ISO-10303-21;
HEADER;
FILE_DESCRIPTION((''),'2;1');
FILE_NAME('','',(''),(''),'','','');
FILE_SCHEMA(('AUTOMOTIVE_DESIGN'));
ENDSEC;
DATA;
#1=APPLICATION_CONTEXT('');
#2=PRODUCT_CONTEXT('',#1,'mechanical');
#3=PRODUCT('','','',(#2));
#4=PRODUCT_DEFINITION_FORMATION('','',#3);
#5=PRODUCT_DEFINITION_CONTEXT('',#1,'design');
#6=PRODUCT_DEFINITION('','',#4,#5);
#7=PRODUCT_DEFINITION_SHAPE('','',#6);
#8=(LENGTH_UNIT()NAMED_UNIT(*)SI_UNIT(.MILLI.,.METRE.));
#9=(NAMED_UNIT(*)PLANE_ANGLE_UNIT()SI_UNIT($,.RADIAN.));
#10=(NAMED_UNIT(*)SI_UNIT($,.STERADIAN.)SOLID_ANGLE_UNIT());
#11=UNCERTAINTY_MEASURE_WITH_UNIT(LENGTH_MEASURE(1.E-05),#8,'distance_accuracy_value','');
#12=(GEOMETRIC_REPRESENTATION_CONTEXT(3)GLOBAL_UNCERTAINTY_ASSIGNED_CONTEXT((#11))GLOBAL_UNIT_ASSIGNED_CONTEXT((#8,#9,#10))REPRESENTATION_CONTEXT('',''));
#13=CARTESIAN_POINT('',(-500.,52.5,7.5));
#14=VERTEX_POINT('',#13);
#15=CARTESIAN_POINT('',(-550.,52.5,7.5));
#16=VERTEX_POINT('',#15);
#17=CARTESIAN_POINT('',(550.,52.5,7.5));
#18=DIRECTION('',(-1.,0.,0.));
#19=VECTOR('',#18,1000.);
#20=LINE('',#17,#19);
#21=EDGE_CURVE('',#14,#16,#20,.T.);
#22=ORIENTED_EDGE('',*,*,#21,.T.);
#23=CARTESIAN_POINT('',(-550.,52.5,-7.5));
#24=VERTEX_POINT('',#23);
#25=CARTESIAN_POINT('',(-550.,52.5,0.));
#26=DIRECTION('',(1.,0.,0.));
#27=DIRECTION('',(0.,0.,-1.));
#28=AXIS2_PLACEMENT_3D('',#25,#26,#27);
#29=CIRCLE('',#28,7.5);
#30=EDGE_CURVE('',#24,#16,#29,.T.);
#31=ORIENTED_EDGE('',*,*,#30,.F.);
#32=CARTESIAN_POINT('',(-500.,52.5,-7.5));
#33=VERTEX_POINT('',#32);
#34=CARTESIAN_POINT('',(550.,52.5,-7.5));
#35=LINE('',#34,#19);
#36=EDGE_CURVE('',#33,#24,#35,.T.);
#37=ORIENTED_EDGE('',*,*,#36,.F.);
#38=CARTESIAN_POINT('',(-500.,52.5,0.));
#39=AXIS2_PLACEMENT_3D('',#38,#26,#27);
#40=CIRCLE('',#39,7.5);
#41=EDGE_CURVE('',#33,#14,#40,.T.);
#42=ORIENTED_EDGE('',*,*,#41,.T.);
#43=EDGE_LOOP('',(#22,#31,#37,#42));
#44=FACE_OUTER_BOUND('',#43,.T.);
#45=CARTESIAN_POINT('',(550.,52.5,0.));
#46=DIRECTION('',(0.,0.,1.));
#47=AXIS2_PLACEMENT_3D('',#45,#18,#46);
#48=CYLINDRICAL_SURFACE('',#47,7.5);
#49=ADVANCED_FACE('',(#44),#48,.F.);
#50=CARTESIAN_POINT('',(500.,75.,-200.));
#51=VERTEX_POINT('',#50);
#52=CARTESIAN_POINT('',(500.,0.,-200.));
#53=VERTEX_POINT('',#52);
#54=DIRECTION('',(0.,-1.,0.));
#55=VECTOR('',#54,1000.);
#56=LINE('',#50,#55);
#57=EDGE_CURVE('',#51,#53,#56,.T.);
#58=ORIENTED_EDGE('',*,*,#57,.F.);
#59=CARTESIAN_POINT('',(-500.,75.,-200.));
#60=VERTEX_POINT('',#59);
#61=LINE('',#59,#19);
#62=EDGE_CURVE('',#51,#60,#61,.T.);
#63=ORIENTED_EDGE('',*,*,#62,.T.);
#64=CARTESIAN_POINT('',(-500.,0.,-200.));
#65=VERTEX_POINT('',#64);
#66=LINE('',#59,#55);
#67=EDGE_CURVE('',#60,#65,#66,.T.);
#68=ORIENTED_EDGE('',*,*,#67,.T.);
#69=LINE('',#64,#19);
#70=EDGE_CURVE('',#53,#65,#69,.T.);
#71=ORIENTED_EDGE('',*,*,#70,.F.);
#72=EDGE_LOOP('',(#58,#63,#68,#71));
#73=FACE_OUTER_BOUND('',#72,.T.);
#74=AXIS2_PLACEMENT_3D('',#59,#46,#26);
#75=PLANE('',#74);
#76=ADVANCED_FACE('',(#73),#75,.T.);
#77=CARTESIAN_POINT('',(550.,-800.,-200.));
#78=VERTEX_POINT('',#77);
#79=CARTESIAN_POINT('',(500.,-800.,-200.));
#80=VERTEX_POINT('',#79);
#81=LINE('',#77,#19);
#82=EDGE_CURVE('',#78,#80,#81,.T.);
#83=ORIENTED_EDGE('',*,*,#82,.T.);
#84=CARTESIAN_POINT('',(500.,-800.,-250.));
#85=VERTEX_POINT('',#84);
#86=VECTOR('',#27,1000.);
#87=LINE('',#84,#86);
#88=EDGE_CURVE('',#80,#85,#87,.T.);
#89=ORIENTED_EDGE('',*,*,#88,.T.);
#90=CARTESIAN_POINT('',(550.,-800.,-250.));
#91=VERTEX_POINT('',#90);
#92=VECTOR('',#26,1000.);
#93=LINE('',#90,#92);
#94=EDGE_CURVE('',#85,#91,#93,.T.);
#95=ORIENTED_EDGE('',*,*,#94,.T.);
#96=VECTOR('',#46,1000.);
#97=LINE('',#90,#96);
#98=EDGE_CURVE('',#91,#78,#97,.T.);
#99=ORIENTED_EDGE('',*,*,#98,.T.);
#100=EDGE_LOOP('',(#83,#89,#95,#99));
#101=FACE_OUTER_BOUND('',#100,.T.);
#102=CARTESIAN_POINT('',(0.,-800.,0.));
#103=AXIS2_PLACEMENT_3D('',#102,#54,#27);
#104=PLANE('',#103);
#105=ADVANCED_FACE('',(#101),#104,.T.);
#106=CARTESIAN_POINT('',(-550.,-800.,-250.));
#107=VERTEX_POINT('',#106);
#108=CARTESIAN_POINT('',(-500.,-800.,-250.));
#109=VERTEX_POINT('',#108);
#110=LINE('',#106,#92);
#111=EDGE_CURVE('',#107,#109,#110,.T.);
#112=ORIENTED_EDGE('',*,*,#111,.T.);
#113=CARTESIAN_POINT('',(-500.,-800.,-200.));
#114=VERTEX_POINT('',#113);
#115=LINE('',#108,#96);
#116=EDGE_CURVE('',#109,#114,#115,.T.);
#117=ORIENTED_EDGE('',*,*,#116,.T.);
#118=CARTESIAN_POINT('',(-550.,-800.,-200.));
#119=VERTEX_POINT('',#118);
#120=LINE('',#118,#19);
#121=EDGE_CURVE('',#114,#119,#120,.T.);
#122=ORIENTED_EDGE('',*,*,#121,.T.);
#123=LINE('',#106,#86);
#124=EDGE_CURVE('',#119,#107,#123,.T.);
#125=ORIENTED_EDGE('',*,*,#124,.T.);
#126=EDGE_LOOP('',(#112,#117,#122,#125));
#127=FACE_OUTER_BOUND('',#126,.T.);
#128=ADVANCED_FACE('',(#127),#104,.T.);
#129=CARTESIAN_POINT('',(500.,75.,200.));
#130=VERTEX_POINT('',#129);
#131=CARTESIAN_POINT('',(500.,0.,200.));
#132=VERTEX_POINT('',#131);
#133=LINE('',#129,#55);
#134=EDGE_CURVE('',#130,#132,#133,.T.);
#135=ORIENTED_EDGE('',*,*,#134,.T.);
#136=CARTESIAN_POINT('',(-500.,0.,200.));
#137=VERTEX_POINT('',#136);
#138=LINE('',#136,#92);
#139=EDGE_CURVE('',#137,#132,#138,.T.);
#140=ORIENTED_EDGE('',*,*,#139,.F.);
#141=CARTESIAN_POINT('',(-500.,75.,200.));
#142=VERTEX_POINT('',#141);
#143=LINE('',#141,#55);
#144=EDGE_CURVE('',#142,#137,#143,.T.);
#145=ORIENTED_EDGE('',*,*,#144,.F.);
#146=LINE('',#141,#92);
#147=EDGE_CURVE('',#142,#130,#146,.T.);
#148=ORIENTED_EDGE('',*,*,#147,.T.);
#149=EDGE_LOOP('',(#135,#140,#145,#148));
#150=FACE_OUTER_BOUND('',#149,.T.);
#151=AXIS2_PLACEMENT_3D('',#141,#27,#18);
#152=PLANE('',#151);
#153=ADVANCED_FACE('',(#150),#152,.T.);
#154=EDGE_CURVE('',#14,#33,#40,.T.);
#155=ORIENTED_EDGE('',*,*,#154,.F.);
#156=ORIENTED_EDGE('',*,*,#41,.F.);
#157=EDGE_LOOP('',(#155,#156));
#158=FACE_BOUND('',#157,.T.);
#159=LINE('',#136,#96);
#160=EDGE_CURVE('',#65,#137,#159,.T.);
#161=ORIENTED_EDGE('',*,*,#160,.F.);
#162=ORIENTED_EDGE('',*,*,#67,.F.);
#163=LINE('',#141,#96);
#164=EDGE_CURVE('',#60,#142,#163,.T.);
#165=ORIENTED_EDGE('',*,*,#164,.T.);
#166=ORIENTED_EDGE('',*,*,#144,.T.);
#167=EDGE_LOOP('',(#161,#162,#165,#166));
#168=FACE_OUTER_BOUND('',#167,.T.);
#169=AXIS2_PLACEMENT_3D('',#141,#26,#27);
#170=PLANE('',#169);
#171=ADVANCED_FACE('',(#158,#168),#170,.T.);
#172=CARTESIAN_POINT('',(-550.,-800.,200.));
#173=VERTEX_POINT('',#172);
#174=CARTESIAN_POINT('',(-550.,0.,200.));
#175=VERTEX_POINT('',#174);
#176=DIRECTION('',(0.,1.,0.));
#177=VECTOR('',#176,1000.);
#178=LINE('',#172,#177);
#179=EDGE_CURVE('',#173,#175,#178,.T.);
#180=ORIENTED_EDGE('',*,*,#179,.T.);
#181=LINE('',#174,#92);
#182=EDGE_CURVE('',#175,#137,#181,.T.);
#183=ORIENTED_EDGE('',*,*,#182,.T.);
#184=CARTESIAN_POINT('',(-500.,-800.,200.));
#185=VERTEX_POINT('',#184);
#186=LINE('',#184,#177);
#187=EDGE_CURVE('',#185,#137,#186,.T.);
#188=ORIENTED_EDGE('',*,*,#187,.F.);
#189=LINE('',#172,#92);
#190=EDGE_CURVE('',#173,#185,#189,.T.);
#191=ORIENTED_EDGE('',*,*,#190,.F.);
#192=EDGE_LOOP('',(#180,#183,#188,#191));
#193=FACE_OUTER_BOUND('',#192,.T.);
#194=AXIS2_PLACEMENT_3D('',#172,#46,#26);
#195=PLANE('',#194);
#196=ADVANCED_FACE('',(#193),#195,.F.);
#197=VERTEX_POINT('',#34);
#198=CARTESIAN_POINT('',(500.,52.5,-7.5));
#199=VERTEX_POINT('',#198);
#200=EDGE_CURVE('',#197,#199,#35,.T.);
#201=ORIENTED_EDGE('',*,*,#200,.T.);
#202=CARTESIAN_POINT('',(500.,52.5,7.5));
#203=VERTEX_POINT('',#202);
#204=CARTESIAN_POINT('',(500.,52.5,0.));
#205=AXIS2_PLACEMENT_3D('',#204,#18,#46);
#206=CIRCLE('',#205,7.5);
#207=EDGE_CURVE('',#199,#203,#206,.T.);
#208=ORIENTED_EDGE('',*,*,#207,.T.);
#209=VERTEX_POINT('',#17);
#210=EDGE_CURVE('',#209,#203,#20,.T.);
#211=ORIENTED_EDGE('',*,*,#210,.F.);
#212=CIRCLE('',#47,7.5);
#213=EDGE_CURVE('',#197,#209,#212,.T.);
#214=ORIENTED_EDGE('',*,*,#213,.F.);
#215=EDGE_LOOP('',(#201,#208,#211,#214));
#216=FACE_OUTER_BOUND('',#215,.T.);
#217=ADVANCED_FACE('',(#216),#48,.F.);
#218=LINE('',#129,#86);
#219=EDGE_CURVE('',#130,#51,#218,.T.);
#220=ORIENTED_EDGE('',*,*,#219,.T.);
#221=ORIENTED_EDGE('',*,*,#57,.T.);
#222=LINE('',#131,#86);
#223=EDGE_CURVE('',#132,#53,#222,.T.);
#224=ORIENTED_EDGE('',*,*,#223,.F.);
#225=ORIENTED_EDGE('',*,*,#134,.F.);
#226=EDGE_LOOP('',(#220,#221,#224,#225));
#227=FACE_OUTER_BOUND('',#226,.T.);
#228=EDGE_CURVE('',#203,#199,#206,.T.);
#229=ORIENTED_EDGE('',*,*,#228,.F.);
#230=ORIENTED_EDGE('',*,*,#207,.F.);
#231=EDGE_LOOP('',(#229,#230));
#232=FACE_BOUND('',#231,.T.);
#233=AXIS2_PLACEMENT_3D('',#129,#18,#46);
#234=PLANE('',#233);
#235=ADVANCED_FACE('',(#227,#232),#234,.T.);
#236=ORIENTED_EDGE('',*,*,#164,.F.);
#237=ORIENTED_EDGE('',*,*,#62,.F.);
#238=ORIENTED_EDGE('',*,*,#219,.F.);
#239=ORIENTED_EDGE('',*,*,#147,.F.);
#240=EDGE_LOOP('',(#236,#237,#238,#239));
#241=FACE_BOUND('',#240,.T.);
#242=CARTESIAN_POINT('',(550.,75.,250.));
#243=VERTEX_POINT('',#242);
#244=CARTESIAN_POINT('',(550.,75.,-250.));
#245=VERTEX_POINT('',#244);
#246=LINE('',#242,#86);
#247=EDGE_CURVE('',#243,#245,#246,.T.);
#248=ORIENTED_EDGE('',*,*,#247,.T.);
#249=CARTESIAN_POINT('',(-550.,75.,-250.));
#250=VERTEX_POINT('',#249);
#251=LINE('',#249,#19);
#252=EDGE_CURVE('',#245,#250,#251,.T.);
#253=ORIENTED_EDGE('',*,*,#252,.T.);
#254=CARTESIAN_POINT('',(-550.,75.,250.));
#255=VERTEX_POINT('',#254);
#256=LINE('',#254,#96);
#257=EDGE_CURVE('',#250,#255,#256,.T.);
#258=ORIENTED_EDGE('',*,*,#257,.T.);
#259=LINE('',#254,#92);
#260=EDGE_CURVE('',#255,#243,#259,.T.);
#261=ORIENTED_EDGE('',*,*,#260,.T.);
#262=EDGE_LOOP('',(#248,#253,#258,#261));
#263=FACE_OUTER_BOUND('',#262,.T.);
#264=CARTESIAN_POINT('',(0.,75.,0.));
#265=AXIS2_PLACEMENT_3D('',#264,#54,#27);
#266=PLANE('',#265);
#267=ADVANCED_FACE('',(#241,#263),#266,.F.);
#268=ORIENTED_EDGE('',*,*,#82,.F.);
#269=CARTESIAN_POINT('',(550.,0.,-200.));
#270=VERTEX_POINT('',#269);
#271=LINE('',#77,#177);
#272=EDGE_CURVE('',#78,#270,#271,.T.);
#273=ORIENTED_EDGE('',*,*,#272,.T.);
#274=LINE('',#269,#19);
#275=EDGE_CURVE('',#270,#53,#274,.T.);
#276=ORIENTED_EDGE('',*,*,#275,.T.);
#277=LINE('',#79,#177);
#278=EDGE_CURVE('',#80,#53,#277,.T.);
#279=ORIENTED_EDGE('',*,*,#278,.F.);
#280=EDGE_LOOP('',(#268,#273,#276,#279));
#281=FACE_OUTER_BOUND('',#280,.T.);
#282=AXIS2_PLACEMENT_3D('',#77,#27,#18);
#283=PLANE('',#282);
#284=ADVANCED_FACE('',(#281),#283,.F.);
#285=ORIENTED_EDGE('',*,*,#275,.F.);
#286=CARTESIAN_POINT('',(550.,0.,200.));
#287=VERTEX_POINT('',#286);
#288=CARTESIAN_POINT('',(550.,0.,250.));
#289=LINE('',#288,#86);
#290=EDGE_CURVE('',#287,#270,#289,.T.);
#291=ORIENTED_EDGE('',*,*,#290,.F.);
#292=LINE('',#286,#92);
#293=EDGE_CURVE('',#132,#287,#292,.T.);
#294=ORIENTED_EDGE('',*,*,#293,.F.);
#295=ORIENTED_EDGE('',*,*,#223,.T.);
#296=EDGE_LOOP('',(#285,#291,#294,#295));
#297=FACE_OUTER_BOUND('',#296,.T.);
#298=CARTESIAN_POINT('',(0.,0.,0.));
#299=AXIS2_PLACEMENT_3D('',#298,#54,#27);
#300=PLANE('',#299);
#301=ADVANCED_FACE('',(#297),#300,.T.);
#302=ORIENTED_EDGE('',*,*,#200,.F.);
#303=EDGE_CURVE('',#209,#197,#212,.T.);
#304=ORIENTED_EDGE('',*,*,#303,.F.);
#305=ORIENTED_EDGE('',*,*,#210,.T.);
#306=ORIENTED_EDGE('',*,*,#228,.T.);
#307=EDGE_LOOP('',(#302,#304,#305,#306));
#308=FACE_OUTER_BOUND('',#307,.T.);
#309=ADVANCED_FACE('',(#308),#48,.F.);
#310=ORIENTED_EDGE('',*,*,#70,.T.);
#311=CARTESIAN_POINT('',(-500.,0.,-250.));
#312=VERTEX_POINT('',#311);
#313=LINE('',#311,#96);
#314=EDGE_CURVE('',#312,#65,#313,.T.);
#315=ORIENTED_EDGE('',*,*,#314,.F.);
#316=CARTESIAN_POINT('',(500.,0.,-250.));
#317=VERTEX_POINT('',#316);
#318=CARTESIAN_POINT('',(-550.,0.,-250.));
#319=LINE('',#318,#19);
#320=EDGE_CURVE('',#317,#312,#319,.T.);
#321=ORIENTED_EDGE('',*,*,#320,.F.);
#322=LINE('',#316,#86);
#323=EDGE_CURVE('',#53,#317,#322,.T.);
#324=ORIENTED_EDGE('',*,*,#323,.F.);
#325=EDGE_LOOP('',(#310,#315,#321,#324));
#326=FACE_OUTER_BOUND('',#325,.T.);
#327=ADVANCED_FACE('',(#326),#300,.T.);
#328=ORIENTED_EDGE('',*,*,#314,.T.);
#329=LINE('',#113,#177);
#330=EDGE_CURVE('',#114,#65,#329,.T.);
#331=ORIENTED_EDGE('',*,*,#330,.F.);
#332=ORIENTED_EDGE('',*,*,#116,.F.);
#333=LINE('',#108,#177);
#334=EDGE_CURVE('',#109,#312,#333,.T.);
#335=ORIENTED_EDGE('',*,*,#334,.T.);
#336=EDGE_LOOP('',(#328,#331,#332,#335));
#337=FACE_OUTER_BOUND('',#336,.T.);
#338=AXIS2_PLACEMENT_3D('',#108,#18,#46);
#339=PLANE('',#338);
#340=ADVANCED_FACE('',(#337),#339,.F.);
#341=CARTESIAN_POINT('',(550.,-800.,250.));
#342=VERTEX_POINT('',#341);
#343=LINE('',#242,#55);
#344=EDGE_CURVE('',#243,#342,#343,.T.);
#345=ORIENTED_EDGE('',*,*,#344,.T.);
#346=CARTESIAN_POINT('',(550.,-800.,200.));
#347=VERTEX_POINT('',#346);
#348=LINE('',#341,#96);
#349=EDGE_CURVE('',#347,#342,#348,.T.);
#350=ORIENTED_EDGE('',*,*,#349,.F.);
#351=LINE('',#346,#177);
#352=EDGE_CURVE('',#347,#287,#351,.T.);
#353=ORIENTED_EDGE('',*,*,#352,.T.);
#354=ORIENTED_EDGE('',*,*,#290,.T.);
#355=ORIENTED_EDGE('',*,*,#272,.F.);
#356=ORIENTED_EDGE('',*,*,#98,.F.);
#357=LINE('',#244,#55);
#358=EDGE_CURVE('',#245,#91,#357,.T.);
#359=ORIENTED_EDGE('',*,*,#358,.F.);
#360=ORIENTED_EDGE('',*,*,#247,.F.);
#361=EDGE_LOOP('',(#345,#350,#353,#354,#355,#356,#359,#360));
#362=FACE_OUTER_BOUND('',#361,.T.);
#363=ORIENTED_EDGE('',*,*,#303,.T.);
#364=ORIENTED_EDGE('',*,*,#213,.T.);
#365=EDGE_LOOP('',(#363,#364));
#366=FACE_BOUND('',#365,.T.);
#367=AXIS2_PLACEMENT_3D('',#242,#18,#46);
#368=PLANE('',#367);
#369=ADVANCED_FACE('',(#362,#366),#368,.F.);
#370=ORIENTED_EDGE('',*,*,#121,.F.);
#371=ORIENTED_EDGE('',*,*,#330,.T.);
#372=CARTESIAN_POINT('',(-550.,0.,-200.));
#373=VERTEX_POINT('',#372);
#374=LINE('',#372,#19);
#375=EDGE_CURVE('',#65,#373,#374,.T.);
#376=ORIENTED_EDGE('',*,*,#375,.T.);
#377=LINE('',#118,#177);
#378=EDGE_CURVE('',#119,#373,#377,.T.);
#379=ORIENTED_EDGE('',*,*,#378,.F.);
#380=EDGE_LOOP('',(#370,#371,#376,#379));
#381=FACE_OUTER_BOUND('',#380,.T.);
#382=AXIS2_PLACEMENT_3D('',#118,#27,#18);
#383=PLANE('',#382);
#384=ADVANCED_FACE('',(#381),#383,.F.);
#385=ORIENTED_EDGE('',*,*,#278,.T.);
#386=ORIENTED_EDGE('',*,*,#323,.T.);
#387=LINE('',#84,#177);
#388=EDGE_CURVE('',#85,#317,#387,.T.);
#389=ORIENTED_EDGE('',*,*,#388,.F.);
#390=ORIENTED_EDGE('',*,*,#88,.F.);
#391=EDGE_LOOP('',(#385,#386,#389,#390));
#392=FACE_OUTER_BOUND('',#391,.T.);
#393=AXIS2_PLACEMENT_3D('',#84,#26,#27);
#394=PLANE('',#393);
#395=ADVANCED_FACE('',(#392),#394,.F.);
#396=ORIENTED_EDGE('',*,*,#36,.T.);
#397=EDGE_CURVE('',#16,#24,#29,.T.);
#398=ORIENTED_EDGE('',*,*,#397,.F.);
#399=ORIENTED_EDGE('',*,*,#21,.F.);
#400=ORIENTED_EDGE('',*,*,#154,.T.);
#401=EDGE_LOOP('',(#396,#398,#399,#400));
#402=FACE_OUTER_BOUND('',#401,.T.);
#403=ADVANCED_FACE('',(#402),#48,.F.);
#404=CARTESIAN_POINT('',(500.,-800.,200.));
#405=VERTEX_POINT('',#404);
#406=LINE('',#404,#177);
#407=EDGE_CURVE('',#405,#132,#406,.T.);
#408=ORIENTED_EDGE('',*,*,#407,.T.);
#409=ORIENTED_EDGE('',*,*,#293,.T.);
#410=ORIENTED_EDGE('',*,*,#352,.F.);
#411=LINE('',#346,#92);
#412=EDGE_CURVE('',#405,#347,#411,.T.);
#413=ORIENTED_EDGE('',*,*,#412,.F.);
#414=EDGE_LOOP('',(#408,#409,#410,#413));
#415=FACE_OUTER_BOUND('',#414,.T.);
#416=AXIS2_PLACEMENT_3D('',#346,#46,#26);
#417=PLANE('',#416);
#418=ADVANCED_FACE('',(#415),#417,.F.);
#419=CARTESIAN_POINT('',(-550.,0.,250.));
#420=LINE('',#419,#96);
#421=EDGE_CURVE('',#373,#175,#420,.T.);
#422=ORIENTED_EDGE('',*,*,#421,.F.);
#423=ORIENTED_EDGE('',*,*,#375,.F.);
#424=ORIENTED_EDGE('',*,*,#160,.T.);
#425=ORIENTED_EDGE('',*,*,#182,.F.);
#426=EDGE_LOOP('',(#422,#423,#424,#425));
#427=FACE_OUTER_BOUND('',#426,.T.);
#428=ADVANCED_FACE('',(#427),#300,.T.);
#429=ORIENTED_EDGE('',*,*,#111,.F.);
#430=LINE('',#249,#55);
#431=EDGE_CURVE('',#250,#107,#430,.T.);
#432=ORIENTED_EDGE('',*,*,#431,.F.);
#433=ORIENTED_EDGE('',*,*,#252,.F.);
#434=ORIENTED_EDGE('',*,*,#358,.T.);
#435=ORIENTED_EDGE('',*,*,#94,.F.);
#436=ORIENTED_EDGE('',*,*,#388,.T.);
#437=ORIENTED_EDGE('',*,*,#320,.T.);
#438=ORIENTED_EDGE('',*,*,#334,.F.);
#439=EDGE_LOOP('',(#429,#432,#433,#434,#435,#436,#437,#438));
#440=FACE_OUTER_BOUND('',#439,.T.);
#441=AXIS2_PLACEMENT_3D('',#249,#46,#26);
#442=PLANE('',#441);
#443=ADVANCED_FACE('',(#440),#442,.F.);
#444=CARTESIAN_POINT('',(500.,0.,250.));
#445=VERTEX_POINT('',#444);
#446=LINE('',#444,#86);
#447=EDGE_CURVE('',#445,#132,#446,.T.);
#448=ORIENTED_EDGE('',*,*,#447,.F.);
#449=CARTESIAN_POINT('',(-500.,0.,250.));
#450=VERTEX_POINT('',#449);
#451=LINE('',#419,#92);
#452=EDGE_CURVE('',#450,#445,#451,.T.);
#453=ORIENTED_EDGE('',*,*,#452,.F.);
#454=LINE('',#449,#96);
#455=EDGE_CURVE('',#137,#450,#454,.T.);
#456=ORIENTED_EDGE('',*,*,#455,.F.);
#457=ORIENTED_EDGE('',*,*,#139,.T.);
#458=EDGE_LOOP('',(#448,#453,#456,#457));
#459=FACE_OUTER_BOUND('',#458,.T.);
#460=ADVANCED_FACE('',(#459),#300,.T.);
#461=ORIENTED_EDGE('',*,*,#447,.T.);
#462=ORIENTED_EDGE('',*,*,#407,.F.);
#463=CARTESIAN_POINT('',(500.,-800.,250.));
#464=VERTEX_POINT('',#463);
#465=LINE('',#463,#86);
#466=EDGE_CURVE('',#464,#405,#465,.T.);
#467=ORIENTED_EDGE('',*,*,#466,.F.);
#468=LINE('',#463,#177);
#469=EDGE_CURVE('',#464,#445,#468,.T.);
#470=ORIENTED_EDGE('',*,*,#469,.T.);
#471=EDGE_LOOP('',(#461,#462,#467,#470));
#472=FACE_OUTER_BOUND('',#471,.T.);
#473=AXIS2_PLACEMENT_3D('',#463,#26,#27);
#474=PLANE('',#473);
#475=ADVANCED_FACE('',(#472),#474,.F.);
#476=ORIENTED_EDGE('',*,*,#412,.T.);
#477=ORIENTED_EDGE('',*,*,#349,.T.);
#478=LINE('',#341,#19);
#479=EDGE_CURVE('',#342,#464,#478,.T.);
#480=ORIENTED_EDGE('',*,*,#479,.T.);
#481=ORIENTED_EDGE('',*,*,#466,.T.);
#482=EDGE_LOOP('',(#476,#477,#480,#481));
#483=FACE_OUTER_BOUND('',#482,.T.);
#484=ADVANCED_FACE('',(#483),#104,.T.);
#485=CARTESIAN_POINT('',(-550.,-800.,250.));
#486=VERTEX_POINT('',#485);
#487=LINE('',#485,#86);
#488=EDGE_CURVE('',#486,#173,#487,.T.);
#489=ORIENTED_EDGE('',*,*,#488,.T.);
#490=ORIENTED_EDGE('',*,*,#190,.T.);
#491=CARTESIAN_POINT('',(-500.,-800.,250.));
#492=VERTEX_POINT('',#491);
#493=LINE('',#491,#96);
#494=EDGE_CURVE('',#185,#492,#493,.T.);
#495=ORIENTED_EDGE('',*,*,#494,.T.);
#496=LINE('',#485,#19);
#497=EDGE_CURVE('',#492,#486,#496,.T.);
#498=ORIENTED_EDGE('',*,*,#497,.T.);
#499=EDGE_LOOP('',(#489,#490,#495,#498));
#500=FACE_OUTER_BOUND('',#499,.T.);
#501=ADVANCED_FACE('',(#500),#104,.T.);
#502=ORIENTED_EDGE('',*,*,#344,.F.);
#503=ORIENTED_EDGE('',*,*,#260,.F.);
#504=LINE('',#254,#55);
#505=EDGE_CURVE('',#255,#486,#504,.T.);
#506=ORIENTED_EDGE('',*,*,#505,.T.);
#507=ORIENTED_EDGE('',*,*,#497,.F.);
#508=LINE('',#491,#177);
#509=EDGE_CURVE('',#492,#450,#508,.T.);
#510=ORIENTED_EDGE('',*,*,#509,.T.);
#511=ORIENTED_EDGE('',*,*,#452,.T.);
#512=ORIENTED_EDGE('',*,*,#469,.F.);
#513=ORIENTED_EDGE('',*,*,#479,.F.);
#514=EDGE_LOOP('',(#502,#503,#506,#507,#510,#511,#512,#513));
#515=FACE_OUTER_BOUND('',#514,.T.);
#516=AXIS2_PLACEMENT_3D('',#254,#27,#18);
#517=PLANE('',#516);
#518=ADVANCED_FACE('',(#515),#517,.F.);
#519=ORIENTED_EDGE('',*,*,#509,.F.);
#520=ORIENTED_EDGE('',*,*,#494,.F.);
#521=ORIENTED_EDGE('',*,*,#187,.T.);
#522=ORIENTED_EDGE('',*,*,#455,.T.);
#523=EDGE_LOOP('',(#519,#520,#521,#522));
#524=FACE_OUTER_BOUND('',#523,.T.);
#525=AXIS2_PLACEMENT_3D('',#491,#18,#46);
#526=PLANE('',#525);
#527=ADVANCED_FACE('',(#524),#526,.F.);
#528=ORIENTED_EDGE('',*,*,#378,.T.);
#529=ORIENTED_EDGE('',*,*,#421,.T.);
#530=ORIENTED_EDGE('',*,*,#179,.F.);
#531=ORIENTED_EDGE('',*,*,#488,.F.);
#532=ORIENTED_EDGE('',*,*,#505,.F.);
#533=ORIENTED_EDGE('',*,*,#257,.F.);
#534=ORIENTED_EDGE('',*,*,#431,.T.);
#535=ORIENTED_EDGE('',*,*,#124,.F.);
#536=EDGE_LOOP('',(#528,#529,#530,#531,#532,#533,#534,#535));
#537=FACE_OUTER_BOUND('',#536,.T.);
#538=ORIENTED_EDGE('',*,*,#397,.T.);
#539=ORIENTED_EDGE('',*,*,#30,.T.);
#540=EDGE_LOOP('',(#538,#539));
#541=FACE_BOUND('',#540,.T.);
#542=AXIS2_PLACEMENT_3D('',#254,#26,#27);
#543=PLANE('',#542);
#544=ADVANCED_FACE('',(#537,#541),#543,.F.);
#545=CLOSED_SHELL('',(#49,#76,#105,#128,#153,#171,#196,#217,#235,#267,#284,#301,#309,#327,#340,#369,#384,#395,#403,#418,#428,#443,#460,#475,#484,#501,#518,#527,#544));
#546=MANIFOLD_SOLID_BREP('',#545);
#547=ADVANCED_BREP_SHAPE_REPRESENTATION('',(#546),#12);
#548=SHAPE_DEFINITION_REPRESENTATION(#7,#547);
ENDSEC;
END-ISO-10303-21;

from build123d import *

# Parameters (mm, degrees)
SKETCH1_W               = 1100
SKETCH1_H               = 500
SKETCH1_W_2             = 1000
SKETCH1_H_2             = 400
BOSS_EXTRUDE1_DEPTH     = 75
SKETCH2_W               = 50
SKETCH2_H               = 50
BOSS_EXTRUDE2_DEPTH     = 800
CUT_EXTRUDE1_DEPTH      = 1383.931668594
CUT_EXTRUDE1_DEPTH_BACK = 1383.931668594
SKETCH3_R               = 7.5


with BuildPart() as part:
    # Sketch1 → Boss-Extrude1 (new body)
    with BuildSketch(Plane(origin=(0, 0, 0), x_dir=(1, 0, 0), z_dir=(0, 1, 0))):
        Rectangle(SKETCH1_W, SKETCH1_H)
        Rectangle(SKETCH1_W_2, SKETCH1_H_2, mode=Mode.SUBTRACT)
    extrude(amount=BOSS_EXTRUDE1_DEPTH)

    # Sketch2 → Boss-Extrude2 (add)
    with BuildSketch(Plane.XZ):
        with Locations((-525, 225)):
            Rectangle(SKETCH2_W, SKETCH2_H)
        with Locations((525, 225)):
            Rectangle(SKETCH2_W, SKETCH2_H)
        with Locations((525, -225)):
            Rectangle(SKETCH2_W, SKETCH2_H)
        with Locations((-525, -225)):
            Rectangle(SKETCH2_W, SKETCH2_H)
    extrude(amount=BOSS_EXTRUDE2_DEPTH)

    # Sketch3 → Cut-Extrude1 (cut, two sides: drawn at the far end of the back side and taken through both)
    with BuildSketch(Plane.ZY.offset(550).offset(-CUT_EXTRUDE1_DEPTH_BACK)):
        with Locations(Location((0, 52.5, 0), (0, 0, 180))):
            Circle(SKETCH3_R)
    extrude(amount=CUT_EXTRUDE1_DEPTH + CUT_EXTRUDE1_DEPTH_BACK, mode=Mode.SUBTRACT)


solid = part.part
